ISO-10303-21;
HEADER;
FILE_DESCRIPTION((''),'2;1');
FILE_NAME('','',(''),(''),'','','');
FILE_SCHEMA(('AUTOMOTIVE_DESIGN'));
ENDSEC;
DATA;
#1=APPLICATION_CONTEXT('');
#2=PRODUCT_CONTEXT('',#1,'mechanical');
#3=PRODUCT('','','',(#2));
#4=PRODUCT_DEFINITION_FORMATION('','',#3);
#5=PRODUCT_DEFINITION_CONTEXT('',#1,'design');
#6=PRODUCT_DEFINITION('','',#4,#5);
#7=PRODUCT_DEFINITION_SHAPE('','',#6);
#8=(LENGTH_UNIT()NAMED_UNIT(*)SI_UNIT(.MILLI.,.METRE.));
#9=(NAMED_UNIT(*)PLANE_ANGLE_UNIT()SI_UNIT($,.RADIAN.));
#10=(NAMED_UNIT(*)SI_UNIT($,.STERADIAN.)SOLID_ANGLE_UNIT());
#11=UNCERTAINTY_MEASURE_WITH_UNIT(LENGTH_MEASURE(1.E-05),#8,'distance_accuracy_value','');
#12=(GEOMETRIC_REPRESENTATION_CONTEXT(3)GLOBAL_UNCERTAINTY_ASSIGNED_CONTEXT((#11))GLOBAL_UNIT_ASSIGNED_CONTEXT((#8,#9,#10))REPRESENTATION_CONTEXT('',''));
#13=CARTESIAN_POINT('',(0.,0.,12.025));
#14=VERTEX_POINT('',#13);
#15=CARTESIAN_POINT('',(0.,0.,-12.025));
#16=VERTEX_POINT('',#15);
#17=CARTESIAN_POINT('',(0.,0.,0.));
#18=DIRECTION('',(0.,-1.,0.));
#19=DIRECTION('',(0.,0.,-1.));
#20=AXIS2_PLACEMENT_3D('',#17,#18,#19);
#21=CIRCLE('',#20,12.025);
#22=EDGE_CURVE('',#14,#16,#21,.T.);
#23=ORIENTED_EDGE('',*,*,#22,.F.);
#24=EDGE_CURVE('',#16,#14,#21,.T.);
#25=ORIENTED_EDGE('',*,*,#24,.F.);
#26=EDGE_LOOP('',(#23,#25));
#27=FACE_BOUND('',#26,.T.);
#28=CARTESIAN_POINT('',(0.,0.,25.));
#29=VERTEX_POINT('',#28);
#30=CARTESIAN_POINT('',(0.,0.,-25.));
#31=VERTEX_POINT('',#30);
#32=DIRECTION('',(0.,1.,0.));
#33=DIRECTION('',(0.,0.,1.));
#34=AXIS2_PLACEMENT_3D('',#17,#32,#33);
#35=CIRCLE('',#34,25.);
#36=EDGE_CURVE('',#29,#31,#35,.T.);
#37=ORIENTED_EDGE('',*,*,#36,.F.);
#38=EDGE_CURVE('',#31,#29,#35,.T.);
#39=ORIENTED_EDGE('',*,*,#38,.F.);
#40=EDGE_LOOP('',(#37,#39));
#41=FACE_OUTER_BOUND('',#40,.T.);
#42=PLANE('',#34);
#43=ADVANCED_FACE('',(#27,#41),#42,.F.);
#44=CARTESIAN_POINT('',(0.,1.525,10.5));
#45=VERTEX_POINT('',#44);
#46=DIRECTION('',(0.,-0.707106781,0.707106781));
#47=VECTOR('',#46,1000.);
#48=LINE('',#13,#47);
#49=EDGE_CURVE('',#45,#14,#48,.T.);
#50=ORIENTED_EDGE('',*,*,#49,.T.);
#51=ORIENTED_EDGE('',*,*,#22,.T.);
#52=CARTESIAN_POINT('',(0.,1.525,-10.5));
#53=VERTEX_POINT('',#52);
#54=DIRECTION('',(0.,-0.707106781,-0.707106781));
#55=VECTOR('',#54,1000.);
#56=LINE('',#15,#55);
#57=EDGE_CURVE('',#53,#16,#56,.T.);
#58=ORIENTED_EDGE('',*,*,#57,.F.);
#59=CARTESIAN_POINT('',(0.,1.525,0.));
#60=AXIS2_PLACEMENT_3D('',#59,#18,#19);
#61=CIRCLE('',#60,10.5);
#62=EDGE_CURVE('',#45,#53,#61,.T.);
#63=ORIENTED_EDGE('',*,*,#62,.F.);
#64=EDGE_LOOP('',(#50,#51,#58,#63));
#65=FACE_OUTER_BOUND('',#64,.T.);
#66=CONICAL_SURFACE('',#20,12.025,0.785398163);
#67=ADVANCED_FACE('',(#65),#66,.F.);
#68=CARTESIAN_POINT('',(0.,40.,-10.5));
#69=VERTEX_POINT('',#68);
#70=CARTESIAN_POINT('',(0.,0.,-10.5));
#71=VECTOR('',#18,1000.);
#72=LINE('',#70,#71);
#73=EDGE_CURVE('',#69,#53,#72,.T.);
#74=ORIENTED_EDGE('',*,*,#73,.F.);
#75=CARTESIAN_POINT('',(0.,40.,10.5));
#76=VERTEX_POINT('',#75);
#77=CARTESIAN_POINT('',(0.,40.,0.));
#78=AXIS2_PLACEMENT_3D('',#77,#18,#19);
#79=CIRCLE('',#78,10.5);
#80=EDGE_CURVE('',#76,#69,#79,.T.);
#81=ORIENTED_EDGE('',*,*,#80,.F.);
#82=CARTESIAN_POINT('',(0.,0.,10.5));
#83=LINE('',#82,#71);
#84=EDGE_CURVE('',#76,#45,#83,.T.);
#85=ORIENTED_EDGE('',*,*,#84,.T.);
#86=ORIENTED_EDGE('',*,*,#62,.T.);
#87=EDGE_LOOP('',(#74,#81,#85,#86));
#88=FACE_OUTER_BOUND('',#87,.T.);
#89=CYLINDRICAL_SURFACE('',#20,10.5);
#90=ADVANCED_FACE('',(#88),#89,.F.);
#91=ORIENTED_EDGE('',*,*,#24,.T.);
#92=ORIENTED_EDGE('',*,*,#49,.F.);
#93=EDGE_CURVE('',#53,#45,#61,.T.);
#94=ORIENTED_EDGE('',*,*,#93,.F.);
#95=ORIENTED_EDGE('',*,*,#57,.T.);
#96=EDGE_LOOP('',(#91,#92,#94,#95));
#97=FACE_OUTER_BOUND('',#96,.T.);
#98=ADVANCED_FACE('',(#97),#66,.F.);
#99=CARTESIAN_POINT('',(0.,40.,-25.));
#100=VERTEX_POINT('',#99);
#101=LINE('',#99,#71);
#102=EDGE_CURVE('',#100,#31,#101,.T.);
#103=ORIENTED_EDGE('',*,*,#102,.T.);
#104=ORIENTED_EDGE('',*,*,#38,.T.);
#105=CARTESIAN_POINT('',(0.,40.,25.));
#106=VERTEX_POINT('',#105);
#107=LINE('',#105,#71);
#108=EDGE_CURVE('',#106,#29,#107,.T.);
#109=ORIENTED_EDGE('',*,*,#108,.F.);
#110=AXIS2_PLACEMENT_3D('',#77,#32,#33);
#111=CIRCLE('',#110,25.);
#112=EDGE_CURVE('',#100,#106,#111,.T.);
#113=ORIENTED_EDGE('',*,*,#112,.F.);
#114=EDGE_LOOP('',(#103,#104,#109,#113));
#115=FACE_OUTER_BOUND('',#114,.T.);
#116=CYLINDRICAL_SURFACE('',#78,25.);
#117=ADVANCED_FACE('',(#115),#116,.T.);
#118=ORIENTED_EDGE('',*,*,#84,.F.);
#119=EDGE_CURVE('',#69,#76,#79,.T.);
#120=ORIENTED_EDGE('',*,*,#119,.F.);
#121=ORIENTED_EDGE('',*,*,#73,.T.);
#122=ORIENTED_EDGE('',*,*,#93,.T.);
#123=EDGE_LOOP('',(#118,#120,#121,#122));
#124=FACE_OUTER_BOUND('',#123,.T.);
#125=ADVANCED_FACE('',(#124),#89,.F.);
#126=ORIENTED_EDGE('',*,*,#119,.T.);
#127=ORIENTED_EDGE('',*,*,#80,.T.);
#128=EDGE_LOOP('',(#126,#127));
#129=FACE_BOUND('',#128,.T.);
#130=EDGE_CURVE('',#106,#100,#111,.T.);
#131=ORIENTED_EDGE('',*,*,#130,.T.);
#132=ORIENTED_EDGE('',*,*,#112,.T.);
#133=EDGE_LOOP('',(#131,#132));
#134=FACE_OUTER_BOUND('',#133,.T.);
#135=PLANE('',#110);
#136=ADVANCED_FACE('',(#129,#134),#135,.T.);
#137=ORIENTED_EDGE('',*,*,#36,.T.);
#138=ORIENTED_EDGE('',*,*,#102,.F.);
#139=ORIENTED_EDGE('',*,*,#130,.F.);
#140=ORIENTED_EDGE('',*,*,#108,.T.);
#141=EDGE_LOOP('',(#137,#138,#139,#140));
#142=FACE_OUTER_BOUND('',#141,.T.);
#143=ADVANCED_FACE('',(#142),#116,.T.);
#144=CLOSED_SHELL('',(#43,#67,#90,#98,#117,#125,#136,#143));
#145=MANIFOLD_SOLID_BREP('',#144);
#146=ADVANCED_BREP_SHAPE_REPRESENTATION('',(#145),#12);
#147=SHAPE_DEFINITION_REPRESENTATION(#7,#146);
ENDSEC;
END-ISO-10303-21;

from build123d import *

# Parameters (mm, degrees)
SKETCH1_R                    = 25
BOSS_EXTRUDE1_DEPTH          = 40
M24_TAPPED_HOLE1_D           = 21
M24_TAPPED_HOLE1_CSINK_D     = 24.05
M24_TAPPED_HOLE1_CSINK_ANGLE = 90


with BuildPart() as part:
    # Sketch1 → Boss-Extrude1 (new body)
    with BuildSketch(Plane(origin=(0, 0, 0), x_dir=(1, 0, 0), z_dir=(0, 1, 0))):
        with Locations(Location((0, 0, 0), (0, 0, 270))):
            Circle(SKETCH1_R)
    extrude(amount=BOSS_EXTRUDE1_DEPTH)

    # M24 Tapped Hole1 (through all)
    with Locations(Plane(origin=(0, 0, 0), x_dir=(-1, 0, 0), z_dir=(0, -1, 0))):
        with Locations((0, 0)):
            CounterSinkHole(M24_TAPPED_HOLE1_D / 2, M24_TAPPED_HOLE1_CSINK_D / 2, counter_sink_angle=M24_TAPPED_HOLE1_CSINK_ANGLE)


solid = part.part
